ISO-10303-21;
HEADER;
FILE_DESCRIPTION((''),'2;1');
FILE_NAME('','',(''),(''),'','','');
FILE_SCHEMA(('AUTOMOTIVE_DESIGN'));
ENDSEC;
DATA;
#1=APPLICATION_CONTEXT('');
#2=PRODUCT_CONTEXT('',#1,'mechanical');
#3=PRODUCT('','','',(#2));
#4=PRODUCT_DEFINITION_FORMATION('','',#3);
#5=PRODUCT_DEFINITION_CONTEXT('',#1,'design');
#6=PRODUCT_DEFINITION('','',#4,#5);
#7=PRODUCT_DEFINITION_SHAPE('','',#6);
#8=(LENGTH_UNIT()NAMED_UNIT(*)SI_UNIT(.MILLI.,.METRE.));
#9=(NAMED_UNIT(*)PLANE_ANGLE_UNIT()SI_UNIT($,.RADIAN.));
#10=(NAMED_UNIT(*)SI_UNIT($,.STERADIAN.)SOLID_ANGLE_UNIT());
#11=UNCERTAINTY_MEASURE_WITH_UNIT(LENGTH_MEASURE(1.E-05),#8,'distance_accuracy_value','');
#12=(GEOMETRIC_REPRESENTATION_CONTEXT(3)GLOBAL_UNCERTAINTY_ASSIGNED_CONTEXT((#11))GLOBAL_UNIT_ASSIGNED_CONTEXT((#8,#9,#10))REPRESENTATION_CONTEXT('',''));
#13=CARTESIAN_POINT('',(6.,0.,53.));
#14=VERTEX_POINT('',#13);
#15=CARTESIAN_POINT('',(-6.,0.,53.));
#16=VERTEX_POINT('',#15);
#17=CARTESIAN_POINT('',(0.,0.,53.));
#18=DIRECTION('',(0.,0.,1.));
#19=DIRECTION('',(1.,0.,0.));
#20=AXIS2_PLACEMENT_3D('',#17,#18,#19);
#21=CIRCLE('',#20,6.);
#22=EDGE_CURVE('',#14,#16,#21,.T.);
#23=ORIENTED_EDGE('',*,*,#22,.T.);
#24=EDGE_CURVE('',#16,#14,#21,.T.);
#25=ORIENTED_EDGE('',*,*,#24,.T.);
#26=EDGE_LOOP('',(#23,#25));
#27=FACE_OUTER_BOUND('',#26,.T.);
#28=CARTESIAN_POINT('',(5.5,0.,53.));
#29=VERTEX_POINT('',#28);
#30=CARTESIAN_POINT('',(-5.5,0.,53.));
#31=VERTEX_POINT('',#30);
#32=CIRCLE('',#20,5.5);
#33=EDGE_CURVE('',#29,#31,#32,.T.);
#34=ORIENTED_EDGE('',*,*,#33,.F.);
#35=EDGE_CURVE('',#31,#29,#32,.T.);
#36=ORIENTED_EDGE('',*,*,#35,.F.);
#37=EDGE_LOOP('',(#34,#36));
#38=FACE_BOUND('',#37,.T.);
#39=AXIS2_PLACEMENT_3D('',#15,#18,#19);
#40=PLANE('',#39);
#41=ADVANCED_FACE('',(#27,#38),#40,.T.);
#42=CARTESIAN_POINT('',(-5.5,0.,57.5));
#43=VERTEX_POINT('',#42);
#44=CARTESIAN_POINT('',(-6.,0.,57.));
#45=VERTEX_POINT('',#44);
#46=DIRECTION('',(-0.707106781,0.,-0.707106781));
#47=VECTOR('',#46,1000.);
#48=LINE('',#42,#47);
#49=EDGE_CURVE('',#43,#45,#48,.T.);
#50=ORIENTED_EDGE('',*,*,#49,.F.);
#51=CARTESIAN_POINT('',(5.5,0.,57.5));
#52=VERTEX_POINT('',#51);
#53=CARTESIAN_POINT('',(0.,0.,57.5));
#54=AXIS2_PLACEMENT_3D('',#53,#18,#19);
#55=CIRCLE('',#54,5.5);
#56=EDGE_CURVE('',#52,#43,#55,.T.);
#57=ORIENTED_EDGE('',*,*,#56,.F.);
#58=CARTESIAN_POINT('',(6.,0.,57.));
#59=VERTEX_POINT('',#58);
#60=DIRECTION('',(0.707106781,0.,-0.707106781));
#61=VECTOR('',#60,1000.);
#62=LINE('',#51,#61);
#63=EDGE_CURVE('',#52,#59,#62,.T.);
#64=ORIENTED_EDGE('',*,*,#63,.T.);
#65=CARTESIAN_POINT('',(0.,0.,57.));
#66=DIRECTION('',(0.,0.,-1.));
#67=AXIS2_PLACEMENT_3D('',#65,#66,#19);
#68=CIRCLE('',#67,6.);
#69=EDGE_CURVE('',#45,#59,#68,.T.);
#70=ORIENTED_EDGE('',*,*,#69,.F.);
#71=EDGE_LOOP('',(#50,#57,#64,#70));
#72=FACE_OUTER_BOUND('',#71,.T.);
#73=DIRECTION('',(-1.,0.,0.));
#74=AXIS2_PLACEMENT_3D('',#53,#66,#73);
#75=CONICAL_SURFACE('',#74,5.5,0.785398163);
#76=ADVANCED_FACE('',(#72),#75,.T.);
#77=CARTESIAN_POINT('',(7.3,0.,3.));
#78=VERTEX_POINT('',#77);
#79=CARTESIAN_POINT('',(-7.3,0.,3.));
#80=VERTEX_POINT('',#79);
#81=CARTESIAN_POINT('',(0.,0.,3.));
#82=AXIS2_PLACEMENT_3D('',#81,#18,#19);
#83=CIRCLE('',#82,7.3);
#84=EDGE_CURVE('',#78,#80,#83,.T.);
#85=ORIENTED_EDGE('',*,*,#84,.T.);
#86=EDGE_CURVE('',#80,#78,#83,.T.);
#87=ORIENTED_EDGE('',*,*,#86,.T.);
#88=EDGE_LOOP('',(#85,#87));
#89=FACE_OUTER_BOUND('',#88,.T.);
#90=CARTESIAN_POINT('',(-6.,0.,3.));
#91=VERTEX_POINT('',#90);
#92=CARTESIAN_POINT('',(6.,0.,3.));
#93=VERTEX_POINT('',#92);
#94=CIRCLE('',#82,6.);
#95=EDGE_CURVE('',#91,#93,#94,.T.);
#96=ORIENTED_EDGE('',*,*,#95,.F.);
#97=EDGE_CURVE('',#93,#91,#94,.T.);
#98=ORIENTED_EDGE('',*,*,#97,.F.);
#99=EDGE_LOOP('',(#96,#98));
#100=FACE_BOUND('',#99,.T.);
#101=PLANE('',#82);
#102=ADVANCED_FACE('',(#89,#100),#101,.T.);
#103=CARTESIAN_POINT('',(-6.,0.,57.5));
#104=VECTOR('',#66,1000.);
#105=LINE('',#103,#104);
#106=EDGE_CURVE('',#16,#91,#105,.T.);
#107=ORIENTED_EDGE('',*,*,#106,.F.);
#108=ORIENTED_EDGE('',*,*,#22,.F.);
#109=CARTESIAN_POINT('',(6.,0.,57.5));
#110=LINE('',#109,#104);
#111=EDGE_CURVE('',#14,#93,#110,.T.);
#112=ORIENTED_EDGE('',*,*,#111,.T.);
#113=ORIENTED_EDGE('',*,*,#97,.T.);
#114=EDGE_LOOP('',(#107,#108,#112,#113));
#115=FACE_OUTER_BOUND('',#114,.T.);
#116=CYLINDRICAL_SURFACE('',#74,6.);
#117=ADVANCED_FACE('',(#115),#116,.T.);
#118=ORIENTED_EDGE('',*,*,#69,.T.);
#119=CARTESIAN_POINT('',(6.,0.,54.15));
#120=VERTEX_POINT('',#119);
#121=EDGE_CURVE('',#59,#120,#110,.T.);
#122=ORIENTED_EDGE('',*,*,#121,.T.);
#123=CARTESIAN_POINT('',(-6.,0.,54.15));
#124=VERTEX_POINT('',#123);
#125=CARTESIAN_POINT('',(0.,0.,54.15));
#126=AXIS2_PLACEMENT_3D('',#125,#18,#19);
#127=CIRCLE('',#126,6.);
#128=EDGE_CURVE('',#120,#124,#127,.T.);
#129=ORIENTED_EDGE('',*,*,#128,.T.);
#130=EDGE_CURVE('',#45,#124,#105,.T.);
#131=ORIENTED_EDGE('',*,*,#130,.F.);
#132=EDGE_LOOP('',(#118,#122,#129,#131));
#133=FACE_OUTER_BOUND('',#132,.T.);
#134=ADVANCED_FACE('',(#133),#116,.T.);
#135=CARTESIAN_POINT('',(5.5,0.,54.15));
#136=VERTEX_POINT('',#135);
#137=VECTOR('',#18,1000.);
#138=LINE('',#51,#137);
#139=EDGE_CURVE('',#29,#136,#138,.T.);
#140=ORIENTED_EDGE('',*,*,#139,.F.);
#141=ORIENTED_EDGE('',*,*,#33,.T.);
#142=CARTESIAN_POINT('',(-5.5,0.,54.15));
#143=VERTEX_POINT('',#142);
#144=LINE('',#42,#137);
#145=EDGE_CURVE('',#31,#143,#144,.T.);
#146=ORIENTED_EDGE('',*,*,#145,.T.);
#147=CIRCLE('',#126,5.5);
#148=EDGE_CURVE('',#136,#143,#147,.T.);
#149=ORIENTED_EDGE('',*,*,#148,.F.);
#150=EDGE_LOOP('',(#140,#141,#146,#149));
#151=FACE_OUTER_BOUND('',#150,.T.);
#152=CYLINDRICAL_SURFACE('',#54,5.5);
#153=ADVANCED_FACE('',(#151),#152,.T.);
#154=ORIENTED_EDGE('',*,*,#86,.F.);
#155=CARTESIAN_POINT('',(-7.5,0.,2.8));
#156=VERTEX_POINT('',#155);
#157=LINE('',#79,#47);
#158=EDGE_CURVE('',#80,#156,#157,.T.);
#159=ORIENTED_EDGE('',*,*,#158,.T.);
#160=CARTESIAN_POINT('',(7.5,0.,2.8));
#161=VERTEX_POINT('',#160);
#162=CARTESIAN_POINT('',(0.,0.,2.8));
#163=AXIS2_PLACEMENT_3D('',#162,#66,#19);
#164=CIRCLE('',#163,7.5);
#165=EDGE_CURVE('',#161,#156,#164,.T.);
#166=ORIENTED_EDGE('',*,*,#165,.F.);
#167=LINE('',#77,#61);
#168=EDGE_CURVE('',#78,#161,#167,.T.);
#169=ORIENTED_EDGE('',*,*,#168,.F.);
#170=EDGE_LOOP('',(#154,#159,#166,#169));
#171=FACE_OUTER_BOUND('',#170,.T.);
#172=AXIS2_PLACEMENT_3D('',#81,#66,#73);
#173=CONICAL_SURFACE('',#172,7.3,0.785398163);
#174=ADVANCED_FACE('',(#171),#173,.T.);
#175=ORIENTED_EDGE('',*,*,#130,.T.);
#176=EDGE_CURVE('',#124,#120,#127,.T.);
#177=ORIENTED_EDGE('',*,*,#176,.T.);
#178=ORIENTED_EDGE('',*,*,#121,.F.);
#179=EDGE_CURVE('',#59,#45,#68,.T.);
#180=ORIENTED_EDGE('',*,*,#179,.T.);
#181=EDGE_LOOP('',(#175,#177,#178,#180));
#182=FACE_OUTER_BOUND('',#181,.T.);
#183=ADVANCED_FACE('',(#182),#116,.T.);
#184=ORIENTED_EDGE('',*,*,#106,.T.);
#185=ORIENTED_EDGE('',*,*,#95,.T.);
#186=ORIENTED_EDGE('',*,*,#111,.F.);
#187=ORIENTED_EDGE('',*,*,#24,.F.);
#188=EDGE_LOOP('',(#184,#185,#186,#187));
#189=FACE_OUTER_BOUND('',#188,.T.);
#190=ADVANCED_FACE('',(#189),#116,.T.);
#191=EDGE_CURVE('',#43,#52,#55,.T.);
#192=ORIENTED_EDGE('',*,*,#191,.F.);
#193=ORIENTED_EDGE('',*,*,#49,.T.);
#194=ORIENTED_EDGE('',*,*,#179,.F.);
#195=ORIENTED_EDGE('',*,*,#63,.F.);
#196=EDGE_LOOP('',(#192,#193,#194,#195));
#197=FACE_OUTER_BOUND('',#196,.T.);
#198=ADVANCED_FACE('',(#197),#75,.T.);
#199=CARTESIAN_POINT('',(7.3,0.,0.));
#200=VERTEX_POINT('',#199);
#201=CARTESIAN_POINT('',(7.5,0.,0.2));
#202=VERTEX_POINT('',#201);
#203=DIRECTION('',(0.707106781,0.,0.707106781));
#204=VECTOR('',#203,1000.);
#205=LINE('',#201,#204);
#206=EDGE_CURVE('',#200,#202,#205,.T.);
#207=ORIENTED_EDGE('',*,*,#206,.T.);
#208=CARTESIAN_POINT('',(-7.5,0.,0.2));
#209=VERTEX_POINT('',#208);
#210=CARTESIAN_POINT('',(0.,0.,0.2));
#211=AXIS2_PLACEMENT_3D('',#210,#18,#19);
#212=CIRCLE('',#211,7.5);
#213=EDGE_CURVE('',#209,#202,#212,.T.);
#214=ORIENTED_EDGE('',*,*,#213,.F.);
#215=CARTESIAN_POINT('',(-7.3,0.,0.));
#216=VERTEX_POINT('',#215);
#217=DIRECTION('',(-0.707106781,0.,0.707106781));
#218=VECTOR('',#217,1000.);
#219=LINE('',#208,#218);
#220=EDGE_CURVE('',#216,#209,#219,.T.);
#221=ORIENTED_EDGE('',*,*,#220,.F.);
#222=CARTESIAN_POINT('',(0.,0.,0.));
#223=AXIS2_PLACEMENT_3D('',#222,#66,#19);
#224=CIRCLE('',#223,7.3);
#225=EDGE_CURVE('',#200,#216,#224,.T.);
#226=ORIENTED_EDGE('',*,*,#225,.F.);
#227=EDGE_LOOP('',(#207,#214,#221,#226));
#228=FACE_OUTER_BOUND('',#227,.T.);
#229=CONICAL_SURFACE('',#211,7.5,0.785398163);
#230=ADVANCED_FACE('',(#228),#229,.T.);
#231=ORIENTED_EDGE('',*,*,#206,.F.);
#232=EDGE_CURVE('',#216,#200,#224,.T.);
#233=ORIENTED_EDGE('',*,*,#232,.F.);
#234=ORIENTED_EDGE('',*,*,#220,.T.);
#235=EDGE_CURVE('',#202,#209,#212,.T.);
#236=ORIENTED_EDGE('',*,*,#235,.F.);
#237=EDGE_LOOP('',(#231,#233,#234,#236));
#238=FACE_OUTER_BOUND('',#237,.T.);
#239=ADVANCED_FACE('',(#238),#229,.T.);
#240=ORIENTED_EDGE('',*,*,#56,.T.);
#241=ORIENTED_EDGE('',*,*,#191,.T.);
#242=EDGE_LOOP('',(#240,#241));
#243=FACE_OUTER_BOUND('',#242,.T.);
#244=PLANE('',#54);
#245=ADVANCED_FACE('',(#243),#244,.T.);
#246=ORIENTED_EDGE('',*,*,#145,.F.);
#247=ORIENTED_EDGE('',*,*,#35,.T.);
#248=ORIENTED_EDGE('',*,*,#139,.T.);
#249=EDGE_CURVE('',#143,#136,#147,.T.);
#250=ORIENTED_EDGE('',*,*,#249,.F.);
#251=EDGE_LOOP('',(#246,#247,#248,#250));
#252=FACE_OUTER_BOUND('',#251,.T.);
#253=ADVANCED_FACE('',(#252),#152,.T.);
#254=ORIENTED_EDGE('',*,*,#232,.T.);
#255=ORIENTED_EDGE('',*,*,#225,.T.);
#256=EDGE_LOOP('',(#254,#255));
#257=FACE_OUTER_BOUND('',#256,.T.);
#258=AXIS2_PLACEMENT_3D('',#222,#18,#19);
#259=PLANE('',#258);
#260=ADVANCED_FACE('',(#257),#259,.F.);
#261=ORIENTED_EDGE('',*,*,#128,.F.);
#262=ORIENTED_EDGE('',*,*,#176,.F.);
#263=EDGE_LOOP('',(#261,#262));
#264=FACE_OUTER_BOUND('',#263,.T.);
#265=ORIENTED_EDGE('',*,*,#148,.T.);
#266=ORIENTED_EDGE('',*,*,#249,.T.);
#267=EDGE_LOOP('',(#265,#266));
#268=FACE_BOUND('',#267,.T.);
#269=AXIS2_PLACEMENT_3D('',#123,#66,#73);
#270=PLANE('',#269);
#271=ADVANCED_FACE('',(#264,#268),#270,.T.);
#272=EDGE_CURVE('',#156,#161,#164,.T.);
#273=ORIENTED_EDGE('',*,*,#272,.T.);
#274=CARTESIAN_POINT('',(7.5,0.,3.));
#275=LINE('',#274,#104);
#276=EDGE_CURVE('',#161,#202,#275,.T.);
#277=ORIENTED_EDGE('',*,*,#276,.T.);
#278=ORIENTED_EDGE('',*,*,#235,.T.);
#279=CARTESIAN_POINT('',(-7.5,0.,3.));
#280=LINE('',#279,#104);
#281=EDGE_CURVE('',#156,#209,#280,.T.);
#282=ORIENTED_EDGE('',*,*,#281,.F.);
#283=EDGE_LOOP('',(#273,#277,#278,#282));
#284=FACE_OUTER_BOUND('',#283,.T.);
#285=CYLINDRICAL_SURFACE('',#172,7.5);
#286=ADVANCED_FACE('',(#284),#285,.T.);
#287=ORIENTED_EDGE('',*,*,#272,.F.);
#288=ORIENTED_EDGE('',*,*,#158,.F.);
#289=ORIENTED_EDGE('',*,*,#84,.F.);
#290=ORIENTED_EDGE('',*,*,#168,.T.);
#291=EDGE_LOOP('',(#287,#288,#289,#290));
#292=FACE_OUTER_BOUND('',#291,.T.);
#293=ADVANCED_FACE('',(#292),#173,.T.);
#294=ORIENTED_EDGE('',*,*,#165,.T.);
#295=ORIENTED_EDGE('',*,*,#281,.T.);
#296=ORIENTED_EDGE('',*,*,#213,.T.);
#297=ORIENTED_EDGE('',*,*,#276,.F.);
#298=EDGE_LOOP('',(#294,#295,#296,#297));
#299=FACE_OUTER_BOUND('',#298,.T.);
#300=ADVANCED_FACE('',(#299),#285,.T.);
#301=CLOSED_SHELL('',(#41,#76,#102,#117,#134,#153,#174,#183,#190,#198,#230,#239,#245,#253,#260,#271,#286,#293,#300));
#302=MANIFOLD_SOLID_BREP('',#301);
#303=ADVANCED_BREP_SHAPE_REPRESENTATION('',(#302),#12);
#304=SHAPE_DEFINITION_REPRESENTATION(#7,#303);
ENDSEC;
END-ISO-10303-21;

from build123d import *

# Parameters (mm, degrees)
SKETCH1_R           = 7.5
BOSS_EXTRUDE1_DEPTH = 3
SKETCH2_R           = 6
BOSS_EXTRUDE2_DEPTH = 54.5
CHAMFER1_SIZE       = 0.2
SKETCH3_W           = 0.5
SKETCH3_H           = 1.15
CHAMFER2_SIZE       = 0.5


with BuildPart() as part:
    # Sketch1 → Boss-Extrude1 (new body)
    with BuildSketch(Plane.XY):
        Circle(SKETCH1_R)
    extrude(amount=BOSS_EXTRUDE1_DEPTH)

    # Sketch2 → Boss-Extrude2 (add)
    with BuildSketch(Plane.XY.offset(3)):
        Circle(SKETCH2_R)
    extrude(amount=BOSS_EXTRUDE2_DEPTH)

    # Chamfer1
    chamfer1_edges = [part.edges().sort_by_distance(p)[0] for p in [
        (-7.5, 0, 0),
        (-7.5, 0, 3),
    ]]
    chamfer(chamfer1_edges, length=CHAMFER1_SIZE)

    # Sketch3 → Cut-Revolve1 (revolve, cut)
    with BuildSketch(Plane(origin=(0, 0, 0), x_dir=(1, 0, 0), z_dir=(0, 1, 0)), mode=Mode.PRIVATE) as cut_revolve1_sk:
        with Locations((-5.75, -53.575)):
            Rectangle(SKETCH3_W, SKETCH3_H)
    revolve(cut_revolve1_sk.sketch.rotate(Axis((0, 0, 57.5), (0, 0, -1)), 180), axis=Axis((0, 0, 57.5), (0, 0, -1)), mode=Mode.SUBTRACT)

    # Chamfer2
    chamfer2_edges = [part.edges().sort_by_distance(p)[0] for p in [
        (-6, 0, 57.5),
    ]]
    chamfer(chamfer2_edges, length=CHAMFER2_SIZE)


solid = part.part
